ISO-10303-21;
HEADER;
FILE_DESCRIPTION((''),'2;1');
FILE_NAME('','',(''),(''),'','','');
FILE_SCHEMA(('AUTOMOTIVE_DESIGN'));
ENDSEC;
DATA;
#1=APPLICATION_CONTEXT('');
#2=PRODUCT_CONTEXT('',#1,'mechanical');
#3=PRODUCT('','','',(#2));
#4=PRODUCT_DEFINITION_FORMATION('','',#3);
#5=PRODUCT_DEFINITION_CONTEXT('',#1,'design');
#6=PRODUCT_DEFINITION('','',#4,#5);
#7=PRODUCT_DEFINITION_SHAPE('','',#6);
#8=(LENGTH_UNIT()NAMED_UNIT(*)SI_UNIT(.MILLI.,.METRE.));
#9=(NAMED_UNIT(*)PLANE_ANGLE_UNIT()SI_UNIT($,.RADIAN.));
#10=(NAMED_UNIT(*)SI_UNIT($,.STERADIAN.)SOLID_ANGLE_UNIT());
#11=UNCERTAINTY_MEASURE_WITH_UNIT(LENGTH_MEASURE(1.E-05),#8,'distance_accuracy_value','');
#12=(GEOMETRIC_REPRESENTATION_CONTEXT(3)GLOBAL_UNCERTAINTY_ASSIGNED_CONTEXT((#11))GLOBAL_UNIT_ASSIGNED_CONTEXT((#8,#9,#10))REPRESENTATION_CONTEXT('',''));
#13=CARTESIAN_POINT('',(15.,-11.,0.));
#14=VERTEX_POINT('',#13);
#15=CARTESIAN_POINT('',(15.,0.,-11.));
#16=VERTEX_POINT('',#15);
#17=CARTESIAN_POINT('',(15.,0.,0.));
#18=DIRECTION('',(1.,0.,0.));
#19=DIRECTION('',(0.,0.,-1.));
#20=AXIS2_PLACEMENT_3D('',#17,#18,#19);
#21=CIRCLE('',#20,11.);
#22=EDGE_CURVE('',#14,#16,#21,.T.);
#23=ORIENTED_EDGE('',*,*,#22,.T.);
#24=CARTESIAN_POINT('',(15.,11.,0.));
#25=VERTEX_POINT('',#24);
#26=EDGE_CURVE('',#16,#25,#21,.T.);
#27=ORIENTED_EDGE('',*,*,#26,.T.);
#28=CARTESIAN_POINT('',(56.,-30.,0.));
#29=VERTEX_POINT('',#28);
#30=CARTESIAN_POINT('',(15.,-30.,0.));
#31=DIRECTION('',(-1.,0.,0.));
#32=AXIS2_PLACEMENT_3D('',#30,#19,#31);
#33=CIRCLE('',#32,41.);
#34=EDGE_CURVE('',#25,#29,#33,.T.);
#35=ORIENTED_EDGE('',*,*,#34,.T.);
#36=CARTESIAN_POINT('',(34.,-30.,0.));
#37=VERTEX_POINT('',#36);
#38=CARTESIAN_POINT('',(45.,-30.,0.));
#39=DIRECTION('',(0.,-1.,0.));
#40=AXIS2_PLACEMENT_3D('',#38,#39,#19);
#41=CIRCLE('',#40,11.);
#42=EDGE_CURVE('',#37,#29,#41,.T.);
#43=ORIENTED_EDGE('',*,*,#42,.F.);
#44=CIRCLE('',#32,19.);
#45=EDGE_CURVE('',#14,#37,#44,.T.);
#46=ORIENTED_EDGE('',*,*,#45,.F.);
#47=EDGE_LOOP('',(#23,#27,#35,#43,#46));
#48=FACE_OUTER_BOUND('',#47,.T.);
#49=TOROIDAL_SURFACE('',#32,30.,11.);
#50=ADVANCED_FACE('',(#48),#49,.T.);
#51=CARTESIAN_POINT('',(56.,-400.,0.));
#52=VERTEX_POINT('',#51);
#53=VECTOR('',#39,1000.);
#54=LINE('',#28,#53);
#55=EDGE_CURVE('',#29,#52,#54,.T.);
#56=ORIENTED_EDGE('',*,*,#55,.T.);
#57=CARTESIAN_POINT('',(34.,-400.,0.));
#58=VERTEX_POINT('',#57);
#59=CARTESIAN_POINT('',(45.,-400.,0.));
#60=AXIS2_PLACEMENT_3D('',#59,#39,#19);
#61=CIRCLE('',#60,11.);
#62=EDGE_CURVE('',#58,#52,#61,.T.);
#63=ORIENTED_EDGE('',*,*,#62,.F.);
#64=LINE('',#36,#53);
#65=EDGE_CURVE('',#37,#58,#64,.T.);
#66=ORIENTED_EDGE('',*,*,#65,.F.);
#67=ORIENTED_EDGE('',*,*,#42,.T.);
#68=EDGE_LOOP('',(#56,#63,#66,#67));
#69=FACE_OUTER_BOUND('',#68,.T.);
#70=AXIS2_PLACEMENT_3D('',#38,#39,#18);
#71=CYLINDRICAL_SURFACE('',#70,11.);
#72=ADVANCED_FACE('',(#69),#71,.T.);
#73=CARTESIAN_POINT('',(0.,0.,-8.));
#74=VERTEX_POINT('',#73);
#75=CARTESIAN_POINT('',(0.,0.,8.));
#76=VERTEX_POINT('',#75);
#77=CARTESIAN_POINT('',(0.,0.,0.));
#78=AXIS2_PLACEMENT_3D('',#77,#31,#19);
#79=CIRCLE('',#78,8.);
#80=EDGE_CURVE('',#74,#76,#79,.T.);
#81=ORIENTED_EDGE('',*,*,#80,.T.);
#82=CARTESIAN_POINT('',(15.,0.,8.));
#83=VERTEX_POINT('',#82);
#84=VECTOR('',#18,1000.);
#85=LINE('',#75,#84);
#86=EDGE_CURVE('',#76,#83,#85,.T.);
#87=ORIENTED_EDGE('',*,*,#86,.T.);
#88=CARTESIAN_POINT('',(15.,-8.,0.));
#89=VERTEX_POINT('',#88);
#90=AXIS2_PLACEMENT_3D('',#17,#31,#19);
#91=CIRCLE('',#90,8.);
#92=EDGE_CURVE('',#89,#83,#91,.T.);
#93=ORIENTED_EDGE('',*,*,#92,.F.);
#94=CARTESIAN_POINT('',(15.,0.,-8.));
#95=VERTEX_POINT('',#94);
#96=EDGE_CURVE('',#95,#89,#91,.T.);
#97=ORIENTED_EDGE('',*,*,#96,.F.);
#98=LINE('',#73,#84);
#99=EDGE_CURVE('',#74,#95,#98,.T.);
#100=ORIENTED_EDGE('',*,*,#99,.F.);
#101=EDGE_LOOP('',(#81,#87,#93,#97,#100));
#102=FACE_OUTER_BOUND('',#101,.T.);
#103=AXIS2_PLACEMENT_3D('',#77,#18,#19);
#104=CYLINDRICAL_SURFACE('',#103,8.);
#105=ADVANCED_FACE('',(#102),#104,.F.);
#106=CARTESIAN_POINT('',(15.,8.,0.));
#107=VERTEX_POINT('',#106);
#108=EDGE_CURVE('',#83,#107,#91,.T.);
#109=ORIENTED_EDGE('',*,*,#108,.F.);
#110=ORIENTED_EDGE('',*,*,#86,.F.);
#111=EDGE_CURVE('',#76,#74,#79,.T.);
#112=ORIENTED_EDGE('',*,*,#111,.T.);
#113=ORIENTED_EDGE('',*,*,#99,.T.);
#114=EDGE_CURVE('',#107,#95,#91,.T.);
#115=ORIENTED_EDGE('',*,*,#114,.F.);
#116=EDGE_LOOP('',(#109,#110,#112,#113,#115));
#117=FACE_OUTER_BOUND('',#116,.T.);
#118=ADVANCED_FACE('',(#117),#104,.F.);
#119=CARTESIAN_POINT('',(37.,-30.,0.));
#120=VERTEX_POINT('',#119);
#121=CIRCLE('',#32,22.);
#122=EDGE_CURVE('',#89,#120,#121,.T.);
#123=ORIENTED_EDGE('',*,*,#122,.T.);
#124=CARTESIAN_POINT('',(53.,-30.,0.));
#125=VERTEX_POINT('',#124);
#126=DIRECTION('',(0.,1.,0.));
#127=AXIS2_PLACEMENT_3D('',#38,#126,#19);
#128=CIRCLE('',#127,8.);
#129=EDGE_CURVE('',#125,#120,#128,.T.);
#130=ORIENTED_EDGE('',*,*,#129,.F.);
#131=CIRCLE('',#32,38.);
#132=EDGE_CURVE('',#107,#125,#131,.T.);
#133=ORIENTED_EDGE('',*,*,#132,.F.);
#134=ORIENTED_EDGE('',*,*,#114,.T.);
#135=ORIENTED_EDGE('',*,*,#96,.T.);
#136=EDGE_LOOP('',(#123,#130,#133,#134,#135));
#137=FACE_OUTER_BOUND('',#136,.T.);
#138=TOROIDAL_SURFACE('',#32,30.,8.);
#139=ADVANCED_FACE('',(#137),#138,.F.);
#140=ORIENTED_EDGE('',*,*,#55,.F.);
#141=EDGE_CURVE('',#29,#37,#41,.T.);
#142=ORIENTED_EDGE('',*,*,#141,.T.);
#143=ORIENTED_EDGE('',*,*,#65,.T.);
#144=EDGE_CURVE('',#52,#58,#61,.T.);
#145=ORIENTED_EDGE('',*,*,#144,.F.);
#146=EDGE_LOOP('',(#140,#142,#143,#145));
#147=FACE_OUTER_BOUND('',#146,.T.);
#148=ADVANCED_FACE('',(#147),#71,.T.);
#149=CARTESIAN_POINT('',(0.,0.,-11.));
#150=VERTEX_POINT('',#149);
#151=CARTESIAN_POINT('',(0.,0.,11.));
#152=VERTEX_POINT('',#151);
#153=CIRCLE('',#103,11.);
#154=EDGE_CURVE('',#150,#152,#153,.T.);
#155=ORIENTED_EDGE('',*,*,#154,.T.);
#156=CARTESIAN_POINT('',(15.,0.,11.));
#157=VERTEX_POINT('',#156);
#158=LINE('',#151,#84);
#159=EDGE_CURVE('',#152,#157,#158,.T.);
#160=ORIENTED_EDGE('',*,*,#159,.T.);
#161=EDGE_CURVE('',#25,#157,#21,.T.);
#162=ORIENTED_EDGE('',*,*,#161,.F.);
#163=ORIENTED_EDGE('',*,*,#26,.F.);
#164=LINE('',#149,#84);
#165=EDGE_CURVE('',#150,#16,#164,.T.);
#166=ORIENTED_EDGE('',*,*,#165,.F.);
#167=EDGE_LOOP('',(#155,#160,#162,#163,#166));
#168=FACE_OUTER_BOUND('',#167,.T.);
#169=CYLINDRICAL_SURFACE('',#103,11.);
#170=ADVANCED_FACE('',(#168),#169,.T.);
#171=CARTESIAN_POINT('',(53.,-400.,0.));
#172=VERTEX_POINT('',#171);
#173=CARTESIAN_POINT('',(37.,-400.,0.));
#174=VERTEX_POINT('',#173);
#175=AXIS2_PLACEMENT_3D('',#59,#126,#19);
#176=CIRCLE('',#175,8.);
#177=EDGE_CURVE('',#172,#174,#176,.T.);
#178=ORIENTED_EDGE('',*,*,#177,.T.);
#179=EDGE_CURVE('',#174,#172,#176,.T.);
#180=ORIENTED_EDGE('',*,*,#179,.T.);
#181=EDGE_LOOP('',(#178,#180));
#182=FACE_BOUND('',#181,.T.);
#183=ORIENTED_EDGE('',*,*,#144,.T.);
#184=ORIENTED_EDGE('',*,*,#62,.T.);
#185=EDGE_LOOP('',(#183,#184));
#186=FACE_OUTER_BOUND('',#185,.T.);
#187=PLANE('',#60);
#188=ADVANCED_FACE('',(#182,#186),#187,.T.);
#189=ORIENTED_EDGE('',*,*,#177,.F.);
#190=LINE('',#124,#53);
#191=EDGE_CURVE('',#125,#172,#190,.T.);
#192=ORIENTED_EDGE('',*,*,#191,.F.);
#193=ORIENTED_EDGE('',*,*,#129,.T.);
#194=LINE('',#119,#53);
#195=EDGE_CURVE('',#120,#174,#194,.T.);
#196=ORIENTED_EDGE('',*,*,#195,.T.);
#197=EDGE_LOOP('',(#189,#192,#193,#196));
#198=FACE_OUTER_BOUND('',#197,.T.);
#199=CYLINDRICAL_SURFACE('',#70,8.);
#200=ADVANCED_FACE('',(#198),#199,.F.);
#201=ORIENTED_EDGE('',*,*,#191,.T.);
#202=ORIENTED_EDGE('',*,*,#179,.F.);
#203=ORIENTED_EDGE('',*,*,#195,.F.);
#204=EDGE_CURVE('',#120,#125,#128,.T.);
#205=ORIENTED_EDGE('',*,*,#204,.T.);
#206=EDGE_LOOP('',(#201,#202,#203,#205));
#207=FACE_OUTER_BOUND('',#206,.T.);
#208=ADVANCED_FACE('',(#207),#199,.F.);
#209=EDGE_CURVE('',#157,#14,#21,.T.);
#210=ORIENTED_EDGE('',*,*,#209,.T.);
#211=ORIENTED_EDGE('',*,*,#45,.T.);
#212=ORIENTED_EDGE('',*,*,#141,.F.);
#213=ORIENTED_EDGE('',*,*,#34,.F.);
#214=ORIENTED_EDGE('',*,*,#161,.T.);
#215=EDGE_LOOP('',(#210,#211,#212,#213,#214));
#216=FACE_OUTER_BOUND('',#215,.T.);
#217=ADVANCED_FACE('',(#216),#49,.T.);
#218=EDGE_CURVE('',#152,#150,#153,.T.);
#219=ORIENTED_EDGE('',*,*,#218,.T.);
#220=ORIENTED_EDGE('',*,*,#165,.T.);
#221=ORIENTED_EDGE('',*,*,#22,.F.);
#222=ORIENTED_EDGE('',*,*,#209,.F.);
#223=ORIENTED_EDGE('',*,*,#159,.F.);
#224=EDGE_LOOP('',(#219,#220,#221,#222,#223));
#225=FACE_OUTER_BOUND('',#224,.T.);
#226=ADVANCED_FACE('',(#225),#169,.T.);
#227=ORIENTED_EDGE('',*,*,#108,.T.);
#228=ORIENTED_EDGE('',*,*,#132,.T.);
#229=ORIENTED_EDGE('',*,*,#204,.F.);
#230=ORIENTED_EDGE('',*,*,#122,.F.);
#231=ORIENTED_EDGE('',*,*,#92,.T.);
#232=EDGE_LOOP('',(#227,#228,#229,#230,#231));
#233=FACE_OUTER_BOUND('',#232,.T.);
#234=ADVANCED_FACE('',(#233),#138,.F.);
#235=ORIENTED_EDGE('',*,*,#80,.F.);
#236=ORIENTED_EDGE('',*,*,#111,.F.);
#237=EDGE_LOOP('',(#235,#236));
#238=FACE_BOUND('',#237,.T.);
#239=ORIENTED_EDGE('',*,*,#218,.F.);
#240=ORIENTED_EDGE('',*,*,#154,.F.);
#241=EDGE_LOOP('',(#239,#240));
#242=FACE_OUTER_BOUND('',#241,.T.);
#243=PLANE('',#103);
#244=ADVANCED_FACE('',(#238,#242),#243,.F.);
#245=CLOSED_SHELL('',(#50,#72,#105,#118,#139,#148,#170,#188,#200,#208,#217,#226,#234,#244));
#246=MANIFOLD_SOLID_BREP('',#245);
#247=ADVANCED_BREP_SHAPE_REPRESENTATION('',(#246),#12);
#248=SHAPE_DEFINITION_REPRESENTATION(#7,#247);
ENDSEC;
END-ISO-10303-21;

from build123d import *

# Parameters (mm, degrees)
SKETCH_2_R   = 11
SKETCH_2_R_2 = 8


with BuildPart() as part:
    # Sweep 1: sweep along a path in Sketch 1
    with BuildLine(Plane.XY) as sweep_1_path:
        Line((0, 0), (15, 0))
        ThreePointArc((15, 0), (36.213203436, -8.786796564), (45, -30))
        Line((45, -30), (45, -400))
    # Sketch 2 → Sweep 1 (sweep)
    with BuildSketch(Plane(origin=(0, 0, 0), x_dir=(0, 0, -1), z_dir=(1, 0, 0))):
        Circle(SKETCH_2_R)
        Circle(SKETCH_2_R_2, mode=Mode.SUBTRACT)
    sweep(path=sweep_1_path.line)


solid = part.part
